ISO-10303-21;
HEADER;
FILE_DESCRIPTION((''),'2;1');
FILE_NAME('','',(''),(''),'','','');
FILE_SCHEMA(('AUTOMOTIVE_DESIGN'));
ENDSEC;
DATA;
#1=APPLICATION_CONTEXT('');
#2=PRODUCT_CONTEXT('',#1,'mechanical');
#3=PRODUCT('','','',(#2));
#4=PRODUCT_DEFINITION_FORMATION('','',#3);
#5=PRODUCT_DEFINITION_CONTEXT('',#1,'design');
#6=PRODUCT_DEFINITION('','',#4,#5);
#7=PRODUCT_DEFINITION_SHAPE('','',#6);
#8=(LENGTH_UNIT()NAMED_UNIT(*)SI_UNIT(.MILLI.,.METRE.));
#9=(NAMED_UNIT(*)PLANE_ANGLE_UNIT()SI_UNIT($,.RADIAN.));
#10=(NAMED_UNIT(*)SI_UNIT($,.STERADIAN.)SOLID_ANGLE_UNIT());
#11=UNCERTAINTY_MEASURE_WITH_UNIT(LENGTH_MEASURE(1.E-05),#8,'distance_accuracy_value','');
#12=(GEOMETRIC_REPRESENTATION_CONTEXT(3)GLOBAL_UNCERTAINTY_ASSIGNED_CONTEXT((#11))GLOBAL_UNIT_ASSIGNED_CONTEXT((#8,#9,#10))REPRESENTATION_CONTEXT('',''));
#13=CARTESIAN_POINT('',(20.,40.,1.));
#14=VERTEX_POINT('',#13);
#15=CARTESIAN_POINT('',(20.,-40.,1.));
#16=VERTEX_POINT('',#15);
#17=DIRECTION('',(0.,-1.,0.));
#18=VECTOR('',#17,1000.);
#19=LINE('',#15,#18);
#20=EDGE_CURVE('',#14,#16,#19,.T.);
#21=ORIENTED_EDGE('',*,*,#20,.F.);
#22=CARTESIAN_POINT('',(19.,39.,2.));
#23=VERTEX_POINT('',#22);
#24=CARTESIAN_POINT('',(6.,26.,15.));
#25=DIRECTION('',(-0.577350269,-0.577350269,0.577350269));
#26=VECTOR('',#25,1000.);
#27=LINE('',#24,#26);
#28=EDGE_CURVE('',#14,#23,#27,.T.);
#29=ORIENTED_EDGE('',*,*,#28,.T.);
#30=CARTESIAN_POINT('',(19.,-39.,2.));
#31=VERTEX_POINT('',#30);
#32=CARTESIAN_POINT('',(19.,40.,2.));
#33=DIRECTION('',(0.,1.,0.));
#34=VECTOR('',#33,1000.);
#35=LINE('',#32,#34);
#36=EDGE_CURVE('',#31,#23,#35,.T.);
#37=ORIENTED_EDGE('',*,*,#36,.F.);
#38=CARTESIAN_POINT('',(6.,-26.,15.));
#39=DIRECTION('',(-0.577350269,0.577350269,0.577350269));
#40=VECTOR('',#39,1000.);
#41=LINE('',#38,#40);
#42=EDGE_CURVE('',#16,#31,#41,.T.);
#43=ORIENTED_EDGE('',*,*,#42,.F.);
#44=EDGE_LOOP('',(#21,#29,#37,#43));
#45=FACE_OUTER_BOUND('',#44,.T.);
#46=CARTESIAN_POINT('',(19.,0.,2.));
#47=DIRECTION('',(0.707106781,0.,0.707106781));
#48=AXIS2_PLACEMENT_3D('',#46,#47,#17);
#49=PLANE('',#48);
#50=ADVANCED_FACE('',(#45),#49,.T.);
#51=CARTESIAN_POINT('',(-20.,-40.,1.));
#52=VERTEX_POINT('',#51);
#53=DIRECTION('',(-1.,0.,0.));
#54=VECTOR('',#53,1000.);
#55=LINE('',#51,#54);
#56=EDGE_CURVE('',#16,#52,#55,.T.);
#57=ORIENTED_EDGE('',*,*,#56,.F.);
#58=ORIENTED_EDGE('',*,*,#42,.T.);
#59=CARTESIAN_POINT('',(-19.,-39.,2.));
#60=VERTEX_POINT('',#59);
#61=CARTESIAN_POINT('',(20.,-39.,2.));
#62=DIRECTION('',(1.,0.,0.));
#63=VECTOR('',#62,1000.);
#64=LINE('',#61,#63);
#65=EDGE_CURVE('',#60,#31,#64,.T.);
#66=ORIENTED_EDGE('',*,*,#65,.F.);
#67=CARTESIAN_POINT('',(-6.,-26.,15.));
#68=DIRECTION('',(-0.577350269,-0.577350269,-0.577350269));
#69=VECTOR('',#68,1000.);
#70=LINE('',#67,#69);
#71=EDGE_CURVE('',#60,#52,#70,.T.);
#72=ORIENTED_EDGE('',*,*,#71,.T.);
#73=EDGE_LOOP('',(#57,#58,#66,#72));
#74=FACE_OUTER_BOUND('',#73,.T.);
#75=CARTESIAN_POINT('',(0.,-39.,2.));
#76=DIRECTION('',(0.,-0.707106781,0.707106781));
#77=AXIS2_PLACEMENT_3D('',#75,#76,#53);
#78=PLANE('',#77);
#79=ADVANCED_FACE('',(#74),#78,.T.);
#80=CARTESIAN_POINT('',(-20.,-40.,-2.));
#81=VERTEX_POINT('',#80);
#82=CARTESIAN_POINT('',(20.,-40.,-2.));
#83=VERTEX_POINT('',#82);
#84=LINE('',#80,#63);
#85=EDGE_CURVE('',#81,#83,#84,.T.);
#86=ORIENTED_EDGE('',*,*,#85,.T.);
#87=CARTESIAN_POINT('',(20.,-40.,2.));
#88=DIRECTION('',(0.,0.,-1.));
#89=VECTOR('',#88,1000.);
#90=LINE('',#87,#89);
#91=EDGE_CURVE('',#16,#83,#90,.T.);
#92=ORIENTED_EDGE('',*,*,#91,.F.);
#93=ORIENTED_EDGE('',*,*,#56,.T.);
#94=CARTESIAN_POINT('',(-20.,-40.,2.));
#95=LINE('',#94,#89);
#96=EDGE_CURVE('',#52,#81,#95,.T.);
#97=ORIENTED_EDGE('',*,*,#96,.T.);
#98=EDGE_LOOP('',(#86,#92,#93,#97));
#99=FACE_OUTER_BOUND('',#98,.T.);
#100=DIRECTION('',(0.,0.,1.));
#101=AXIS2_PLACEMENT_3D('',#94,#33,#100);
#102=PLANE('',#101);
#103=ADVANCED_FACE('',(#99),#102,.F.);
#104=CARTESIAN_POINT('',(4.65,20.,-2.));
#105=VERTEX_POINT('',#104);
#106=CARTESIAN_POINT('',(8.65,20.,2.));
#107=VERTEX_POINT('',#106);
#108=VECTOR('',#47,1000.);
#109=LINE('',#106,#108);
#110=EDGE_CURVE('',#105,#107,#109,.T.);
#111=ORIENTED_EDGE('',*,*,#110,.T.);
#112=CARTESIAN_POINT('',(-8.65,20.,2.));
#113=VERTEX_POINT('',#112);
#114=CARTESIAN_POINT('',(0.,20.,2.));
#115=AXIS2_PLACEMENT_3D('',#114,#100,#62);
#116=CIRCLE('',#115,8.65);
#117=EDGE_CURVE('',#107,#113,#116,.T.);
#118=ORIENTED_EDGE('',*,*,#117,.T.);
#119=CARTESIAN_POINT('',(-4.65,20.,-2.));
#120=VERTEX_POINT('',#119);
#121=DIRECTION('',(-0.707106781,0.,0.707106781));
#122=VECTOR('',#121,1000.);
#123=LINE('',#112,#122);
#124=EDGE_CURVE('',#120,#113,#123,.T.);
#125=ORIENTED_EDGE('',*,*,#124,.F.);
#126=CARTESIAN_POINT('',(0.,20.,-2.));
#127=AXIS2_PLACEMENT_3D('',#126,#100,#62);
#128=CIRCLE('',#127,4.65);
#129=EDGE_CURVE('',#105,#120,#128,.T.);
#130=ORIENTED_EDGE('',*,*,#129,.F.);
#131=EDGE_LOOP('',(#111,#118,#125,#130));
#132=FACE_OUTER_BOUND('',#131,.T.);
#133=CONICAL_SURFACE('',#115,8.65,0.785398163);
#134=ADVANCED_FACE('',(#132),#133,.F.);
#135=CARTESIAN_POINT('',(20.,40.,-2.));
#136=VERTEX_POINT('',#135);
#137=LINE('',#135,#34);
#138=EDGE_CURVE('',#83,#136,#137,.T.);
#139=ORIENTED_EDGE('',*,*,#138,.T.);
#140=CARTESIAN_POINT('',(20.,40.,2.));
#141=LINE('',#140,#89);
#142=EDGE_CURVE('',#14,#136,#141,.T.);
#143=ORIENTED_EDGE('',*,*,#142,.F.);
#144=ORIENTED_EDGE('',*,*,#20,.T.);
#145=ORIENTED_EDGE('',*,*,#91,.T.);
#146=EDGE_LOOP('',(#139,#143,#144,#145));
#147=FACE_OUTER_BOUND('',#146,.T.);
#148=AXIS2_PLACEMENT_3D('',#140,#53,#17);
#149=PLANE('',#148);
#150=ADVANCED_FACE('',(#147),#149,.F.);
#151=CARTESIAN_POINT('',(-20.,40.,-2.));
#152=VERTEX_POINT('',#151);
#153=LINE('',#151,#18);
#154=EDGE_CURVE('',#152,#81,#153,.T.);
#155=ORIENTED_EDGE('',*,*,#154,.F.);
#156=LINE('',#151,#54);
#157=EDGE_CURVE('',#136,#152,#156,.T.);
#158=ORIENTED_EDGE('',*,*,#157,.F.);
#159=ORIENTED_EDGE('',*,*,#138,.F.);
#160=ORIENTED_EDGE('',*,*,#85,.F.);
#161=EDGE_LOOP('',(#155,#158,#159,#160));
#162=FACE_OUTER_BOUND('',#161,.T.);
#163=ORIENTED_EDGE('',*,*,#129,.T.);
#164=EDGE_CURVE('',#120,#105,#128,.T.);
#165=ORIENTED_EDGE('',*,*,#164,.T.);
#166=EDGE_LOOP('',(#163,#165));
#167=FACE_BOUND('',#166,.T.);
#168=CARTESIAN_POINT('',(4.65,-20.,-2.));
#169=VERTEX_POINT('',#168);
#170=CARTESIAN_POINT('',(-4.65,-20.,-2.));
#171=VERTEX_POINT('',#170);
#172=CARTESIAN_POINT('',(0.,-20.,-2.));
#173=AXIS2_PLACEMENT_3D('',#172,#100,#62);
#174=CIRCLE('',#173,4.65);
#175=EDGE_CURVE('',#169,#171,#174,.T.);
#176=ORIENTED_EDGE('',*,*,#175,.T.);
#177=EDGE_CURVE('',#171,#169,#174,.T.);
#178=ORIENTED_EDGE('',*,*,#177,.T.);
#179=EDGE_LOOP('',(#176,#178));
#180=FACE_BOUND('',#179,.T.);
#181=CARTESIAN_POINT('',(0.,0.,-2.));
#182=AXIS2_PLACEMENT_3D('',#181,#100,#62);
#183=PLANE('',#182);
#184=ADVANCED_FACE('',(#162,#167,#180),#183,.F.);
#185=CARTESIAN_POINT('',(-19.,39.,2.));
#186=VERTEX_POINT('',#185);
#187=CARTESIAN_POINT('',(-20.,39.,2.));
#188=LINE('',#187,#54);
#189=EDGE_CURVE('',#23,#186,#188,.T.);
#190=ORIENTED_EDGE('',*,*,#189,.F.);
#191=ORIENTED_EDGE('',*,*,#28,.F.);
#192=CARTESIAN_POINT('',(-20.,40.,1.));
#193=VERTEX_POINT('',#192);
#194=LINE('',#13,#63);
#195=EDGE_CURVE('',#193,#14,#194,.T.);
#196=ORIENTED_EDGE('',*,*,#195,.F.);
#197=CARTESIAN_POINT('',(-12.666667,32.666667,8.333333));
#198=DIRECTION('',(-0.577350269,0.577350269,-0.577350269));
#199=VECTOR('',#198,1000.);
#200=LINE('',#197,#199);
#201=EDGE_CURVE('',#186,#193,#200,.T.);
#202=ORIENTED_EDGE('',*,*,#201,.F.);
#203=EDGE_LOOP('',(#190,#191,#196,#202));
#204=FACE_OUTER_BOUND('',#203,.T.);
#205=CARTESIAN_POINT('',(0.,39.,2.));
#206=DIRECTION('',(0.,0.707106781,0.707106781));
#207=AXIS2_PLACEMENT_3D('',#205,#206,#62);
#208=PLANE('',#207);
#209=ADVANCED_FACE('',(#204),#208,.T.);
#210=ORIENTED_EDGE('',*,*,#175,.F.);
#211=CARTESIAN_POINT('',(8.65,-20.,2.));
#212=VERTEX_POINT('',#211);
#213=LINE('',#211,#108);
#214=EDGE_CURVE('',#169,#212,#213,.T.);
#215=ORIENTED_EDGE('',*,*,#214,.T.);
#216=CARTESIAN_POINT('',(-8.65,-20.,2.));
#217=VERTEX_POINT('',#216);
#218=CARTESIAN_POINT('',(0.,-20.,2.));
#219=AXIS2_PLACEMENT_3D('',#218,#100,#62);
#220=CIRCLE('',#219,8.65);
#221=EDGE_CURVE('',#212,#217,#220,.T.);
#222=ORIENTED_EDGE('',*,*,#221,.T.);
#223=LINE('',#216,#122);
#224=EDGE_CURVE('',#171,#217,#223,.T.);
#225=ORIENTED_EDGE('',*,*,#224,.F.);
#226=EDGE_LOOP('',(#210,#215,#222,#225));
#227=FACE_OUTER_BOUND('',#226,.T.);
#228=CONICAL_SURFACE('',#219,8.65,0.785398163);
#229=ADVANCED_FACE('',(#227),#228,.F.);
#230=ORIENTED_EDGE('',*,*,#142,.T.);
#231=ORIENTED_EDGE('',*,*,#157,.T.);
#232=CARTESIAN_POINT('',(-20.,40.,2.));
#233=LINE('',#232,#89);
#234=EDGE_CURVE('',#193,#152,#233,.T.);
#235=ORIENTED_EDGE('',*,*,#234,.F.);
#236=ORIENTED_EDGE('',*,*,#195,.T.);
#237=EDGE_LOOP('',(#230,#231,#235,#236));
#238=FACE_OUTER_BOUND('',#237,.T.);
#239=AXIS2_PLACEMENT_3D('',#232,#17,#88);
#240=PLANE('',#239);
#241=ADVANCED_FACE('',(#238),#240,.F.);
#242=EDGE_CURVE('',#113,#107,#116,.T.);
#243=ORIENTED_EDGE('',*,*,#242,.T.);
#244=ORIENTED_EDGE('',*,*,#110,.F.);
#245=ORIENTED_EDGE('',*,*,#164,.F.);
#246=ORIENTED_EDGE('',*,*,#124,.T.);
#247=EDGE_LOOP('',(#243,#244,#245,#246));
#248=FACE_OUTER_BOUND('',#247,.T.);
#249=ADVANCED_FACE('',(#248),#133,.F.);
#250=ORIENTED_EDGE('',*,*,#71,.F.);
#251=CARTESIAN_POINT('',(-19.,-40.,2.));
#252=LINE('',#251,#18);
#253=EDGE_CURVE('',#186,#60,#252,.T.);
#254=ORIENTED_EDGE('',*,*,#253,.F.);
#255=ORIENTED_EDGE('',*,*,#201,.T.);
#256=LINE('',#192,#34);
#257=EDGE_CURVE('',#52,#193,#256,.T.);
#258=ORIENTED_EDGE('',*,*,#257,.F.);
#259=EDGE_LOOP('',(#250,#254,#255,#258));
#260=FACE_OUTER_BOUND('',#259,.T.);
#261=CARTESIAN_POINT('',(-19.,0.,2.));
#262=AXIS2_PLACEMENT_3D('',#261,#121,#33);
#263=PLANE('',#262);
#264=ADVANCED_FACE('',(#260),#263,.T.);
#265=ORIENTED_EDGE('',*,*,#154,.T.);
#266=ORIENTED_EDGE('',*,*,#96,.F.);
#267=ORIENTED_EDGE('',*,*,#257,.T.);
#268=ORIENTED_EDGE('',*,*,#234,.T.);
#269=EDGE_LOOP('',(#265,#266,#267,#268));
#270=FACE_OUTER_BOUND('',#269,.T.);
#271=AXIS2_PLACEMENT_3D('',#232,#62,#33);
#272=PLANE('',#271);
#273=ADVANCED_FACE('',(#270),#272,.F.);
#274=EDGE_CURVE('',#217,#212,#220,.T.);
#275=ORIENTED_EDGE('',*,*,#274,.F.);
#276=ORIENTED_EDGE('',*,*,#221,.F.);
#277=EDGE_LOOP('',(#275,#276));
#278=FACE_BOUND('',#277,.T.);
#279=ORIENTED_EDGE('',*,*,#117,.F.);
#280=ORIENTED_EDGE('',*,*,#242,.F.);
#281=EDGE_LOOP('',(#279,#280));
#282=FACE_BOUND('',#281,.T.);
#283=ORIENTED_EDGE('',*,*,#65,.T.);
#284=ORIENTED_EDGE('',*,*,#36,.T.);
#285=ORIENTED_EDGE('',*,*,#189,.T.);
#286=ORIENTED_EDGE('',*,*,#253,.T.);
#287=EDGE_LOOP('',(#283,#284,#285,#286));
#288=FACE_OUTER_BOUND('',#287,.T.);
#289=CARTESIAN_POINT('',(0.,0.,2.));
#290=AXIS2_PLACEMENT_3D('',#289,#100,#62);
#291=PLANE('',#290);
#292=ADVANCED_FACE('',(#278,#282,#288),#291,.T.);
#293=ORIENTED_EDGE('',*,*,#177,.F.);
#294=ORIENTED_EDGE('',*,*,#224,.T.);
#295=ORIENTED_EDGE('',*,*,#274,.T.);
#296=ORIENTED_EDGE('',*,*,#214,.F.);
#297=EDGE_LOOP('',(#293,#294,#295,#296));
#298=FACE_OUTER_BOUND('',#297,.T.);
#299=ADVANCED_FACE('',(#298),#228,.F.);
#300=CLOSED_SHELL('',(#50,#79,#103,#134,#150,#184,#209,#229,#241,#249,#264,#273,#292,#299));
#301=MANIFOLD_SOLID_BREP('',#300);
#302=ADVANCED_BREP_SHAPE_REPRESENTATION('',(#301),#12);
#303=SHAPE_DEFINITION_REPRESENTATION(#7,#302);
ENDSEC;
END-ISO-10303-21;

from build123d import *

# Parameters (mm, degrees)
SKETCH_1_W                = 40
SKETCH_1_H                = 80
EXTRUDE_1_DEPTH           = 2
HOLE_WIZARD_1_D           = 9
HOLE_WIZARD_1_DEPTH       = 10
HOLE_WIZARD_1_CSINK_D     = 17.3
HOLE_WIZARD_1_CSINK_ANGLE = 90
HOLE_WIZARD_1_TIP         = 2.703872786
CHAMFER_1_SIZE            = 1


with BuildPart() as part:
    # 草图1 → 凸台-拉伸1 (new, symmetric)
    with BuildSketch(Plane.XY):
        Rectangle(SKETCH_1_W, SKETCH_1_H)
    extrude(amount=EXTRUDE_1_DEPTH, both=True)

    # 打孔尺寸(%根据十字)槽沉头木螺钉的类型1
    with Locations(Plane(origin=(0, 20, 2), x_dir=(1, 0, 0), z_dir=(0, 0, 1))):
        with Locations((0, 0), (0, -40)):
            CounterSinkHole(HOLE_WIZARD_1_D / 2, HOLE_WIZARD_1_CSINK_D / 2, depth=HOLE_WIZARD_1_DEPTH, counter_sink_angle=HOLE_WIZARD_1_CSINK_ANGLE)
            with Locations((0, 0, -(HOLE_WIZARD_1_DEPTH + HOLE_WIZARD_1_TIP / 2))):  # 118° drill point
                Cone(0, HOLE_WIZARD_1_D / 2, HOLE_WIZARD_1_TIP, mode=Mode.SUBTRACT)

    # 倒角1
    chamfer_1_edges = [part.edges().sort_by_distance(p)[0] for p in [
        (-20, 0, 2),
        (0, -40, 2),
        (20, 0, 2),
        (0, 40, 2),
    ]]
    chamfer(chamfer_1_edges, length=CHAMFER_1_SIZE)


solid = part.part
